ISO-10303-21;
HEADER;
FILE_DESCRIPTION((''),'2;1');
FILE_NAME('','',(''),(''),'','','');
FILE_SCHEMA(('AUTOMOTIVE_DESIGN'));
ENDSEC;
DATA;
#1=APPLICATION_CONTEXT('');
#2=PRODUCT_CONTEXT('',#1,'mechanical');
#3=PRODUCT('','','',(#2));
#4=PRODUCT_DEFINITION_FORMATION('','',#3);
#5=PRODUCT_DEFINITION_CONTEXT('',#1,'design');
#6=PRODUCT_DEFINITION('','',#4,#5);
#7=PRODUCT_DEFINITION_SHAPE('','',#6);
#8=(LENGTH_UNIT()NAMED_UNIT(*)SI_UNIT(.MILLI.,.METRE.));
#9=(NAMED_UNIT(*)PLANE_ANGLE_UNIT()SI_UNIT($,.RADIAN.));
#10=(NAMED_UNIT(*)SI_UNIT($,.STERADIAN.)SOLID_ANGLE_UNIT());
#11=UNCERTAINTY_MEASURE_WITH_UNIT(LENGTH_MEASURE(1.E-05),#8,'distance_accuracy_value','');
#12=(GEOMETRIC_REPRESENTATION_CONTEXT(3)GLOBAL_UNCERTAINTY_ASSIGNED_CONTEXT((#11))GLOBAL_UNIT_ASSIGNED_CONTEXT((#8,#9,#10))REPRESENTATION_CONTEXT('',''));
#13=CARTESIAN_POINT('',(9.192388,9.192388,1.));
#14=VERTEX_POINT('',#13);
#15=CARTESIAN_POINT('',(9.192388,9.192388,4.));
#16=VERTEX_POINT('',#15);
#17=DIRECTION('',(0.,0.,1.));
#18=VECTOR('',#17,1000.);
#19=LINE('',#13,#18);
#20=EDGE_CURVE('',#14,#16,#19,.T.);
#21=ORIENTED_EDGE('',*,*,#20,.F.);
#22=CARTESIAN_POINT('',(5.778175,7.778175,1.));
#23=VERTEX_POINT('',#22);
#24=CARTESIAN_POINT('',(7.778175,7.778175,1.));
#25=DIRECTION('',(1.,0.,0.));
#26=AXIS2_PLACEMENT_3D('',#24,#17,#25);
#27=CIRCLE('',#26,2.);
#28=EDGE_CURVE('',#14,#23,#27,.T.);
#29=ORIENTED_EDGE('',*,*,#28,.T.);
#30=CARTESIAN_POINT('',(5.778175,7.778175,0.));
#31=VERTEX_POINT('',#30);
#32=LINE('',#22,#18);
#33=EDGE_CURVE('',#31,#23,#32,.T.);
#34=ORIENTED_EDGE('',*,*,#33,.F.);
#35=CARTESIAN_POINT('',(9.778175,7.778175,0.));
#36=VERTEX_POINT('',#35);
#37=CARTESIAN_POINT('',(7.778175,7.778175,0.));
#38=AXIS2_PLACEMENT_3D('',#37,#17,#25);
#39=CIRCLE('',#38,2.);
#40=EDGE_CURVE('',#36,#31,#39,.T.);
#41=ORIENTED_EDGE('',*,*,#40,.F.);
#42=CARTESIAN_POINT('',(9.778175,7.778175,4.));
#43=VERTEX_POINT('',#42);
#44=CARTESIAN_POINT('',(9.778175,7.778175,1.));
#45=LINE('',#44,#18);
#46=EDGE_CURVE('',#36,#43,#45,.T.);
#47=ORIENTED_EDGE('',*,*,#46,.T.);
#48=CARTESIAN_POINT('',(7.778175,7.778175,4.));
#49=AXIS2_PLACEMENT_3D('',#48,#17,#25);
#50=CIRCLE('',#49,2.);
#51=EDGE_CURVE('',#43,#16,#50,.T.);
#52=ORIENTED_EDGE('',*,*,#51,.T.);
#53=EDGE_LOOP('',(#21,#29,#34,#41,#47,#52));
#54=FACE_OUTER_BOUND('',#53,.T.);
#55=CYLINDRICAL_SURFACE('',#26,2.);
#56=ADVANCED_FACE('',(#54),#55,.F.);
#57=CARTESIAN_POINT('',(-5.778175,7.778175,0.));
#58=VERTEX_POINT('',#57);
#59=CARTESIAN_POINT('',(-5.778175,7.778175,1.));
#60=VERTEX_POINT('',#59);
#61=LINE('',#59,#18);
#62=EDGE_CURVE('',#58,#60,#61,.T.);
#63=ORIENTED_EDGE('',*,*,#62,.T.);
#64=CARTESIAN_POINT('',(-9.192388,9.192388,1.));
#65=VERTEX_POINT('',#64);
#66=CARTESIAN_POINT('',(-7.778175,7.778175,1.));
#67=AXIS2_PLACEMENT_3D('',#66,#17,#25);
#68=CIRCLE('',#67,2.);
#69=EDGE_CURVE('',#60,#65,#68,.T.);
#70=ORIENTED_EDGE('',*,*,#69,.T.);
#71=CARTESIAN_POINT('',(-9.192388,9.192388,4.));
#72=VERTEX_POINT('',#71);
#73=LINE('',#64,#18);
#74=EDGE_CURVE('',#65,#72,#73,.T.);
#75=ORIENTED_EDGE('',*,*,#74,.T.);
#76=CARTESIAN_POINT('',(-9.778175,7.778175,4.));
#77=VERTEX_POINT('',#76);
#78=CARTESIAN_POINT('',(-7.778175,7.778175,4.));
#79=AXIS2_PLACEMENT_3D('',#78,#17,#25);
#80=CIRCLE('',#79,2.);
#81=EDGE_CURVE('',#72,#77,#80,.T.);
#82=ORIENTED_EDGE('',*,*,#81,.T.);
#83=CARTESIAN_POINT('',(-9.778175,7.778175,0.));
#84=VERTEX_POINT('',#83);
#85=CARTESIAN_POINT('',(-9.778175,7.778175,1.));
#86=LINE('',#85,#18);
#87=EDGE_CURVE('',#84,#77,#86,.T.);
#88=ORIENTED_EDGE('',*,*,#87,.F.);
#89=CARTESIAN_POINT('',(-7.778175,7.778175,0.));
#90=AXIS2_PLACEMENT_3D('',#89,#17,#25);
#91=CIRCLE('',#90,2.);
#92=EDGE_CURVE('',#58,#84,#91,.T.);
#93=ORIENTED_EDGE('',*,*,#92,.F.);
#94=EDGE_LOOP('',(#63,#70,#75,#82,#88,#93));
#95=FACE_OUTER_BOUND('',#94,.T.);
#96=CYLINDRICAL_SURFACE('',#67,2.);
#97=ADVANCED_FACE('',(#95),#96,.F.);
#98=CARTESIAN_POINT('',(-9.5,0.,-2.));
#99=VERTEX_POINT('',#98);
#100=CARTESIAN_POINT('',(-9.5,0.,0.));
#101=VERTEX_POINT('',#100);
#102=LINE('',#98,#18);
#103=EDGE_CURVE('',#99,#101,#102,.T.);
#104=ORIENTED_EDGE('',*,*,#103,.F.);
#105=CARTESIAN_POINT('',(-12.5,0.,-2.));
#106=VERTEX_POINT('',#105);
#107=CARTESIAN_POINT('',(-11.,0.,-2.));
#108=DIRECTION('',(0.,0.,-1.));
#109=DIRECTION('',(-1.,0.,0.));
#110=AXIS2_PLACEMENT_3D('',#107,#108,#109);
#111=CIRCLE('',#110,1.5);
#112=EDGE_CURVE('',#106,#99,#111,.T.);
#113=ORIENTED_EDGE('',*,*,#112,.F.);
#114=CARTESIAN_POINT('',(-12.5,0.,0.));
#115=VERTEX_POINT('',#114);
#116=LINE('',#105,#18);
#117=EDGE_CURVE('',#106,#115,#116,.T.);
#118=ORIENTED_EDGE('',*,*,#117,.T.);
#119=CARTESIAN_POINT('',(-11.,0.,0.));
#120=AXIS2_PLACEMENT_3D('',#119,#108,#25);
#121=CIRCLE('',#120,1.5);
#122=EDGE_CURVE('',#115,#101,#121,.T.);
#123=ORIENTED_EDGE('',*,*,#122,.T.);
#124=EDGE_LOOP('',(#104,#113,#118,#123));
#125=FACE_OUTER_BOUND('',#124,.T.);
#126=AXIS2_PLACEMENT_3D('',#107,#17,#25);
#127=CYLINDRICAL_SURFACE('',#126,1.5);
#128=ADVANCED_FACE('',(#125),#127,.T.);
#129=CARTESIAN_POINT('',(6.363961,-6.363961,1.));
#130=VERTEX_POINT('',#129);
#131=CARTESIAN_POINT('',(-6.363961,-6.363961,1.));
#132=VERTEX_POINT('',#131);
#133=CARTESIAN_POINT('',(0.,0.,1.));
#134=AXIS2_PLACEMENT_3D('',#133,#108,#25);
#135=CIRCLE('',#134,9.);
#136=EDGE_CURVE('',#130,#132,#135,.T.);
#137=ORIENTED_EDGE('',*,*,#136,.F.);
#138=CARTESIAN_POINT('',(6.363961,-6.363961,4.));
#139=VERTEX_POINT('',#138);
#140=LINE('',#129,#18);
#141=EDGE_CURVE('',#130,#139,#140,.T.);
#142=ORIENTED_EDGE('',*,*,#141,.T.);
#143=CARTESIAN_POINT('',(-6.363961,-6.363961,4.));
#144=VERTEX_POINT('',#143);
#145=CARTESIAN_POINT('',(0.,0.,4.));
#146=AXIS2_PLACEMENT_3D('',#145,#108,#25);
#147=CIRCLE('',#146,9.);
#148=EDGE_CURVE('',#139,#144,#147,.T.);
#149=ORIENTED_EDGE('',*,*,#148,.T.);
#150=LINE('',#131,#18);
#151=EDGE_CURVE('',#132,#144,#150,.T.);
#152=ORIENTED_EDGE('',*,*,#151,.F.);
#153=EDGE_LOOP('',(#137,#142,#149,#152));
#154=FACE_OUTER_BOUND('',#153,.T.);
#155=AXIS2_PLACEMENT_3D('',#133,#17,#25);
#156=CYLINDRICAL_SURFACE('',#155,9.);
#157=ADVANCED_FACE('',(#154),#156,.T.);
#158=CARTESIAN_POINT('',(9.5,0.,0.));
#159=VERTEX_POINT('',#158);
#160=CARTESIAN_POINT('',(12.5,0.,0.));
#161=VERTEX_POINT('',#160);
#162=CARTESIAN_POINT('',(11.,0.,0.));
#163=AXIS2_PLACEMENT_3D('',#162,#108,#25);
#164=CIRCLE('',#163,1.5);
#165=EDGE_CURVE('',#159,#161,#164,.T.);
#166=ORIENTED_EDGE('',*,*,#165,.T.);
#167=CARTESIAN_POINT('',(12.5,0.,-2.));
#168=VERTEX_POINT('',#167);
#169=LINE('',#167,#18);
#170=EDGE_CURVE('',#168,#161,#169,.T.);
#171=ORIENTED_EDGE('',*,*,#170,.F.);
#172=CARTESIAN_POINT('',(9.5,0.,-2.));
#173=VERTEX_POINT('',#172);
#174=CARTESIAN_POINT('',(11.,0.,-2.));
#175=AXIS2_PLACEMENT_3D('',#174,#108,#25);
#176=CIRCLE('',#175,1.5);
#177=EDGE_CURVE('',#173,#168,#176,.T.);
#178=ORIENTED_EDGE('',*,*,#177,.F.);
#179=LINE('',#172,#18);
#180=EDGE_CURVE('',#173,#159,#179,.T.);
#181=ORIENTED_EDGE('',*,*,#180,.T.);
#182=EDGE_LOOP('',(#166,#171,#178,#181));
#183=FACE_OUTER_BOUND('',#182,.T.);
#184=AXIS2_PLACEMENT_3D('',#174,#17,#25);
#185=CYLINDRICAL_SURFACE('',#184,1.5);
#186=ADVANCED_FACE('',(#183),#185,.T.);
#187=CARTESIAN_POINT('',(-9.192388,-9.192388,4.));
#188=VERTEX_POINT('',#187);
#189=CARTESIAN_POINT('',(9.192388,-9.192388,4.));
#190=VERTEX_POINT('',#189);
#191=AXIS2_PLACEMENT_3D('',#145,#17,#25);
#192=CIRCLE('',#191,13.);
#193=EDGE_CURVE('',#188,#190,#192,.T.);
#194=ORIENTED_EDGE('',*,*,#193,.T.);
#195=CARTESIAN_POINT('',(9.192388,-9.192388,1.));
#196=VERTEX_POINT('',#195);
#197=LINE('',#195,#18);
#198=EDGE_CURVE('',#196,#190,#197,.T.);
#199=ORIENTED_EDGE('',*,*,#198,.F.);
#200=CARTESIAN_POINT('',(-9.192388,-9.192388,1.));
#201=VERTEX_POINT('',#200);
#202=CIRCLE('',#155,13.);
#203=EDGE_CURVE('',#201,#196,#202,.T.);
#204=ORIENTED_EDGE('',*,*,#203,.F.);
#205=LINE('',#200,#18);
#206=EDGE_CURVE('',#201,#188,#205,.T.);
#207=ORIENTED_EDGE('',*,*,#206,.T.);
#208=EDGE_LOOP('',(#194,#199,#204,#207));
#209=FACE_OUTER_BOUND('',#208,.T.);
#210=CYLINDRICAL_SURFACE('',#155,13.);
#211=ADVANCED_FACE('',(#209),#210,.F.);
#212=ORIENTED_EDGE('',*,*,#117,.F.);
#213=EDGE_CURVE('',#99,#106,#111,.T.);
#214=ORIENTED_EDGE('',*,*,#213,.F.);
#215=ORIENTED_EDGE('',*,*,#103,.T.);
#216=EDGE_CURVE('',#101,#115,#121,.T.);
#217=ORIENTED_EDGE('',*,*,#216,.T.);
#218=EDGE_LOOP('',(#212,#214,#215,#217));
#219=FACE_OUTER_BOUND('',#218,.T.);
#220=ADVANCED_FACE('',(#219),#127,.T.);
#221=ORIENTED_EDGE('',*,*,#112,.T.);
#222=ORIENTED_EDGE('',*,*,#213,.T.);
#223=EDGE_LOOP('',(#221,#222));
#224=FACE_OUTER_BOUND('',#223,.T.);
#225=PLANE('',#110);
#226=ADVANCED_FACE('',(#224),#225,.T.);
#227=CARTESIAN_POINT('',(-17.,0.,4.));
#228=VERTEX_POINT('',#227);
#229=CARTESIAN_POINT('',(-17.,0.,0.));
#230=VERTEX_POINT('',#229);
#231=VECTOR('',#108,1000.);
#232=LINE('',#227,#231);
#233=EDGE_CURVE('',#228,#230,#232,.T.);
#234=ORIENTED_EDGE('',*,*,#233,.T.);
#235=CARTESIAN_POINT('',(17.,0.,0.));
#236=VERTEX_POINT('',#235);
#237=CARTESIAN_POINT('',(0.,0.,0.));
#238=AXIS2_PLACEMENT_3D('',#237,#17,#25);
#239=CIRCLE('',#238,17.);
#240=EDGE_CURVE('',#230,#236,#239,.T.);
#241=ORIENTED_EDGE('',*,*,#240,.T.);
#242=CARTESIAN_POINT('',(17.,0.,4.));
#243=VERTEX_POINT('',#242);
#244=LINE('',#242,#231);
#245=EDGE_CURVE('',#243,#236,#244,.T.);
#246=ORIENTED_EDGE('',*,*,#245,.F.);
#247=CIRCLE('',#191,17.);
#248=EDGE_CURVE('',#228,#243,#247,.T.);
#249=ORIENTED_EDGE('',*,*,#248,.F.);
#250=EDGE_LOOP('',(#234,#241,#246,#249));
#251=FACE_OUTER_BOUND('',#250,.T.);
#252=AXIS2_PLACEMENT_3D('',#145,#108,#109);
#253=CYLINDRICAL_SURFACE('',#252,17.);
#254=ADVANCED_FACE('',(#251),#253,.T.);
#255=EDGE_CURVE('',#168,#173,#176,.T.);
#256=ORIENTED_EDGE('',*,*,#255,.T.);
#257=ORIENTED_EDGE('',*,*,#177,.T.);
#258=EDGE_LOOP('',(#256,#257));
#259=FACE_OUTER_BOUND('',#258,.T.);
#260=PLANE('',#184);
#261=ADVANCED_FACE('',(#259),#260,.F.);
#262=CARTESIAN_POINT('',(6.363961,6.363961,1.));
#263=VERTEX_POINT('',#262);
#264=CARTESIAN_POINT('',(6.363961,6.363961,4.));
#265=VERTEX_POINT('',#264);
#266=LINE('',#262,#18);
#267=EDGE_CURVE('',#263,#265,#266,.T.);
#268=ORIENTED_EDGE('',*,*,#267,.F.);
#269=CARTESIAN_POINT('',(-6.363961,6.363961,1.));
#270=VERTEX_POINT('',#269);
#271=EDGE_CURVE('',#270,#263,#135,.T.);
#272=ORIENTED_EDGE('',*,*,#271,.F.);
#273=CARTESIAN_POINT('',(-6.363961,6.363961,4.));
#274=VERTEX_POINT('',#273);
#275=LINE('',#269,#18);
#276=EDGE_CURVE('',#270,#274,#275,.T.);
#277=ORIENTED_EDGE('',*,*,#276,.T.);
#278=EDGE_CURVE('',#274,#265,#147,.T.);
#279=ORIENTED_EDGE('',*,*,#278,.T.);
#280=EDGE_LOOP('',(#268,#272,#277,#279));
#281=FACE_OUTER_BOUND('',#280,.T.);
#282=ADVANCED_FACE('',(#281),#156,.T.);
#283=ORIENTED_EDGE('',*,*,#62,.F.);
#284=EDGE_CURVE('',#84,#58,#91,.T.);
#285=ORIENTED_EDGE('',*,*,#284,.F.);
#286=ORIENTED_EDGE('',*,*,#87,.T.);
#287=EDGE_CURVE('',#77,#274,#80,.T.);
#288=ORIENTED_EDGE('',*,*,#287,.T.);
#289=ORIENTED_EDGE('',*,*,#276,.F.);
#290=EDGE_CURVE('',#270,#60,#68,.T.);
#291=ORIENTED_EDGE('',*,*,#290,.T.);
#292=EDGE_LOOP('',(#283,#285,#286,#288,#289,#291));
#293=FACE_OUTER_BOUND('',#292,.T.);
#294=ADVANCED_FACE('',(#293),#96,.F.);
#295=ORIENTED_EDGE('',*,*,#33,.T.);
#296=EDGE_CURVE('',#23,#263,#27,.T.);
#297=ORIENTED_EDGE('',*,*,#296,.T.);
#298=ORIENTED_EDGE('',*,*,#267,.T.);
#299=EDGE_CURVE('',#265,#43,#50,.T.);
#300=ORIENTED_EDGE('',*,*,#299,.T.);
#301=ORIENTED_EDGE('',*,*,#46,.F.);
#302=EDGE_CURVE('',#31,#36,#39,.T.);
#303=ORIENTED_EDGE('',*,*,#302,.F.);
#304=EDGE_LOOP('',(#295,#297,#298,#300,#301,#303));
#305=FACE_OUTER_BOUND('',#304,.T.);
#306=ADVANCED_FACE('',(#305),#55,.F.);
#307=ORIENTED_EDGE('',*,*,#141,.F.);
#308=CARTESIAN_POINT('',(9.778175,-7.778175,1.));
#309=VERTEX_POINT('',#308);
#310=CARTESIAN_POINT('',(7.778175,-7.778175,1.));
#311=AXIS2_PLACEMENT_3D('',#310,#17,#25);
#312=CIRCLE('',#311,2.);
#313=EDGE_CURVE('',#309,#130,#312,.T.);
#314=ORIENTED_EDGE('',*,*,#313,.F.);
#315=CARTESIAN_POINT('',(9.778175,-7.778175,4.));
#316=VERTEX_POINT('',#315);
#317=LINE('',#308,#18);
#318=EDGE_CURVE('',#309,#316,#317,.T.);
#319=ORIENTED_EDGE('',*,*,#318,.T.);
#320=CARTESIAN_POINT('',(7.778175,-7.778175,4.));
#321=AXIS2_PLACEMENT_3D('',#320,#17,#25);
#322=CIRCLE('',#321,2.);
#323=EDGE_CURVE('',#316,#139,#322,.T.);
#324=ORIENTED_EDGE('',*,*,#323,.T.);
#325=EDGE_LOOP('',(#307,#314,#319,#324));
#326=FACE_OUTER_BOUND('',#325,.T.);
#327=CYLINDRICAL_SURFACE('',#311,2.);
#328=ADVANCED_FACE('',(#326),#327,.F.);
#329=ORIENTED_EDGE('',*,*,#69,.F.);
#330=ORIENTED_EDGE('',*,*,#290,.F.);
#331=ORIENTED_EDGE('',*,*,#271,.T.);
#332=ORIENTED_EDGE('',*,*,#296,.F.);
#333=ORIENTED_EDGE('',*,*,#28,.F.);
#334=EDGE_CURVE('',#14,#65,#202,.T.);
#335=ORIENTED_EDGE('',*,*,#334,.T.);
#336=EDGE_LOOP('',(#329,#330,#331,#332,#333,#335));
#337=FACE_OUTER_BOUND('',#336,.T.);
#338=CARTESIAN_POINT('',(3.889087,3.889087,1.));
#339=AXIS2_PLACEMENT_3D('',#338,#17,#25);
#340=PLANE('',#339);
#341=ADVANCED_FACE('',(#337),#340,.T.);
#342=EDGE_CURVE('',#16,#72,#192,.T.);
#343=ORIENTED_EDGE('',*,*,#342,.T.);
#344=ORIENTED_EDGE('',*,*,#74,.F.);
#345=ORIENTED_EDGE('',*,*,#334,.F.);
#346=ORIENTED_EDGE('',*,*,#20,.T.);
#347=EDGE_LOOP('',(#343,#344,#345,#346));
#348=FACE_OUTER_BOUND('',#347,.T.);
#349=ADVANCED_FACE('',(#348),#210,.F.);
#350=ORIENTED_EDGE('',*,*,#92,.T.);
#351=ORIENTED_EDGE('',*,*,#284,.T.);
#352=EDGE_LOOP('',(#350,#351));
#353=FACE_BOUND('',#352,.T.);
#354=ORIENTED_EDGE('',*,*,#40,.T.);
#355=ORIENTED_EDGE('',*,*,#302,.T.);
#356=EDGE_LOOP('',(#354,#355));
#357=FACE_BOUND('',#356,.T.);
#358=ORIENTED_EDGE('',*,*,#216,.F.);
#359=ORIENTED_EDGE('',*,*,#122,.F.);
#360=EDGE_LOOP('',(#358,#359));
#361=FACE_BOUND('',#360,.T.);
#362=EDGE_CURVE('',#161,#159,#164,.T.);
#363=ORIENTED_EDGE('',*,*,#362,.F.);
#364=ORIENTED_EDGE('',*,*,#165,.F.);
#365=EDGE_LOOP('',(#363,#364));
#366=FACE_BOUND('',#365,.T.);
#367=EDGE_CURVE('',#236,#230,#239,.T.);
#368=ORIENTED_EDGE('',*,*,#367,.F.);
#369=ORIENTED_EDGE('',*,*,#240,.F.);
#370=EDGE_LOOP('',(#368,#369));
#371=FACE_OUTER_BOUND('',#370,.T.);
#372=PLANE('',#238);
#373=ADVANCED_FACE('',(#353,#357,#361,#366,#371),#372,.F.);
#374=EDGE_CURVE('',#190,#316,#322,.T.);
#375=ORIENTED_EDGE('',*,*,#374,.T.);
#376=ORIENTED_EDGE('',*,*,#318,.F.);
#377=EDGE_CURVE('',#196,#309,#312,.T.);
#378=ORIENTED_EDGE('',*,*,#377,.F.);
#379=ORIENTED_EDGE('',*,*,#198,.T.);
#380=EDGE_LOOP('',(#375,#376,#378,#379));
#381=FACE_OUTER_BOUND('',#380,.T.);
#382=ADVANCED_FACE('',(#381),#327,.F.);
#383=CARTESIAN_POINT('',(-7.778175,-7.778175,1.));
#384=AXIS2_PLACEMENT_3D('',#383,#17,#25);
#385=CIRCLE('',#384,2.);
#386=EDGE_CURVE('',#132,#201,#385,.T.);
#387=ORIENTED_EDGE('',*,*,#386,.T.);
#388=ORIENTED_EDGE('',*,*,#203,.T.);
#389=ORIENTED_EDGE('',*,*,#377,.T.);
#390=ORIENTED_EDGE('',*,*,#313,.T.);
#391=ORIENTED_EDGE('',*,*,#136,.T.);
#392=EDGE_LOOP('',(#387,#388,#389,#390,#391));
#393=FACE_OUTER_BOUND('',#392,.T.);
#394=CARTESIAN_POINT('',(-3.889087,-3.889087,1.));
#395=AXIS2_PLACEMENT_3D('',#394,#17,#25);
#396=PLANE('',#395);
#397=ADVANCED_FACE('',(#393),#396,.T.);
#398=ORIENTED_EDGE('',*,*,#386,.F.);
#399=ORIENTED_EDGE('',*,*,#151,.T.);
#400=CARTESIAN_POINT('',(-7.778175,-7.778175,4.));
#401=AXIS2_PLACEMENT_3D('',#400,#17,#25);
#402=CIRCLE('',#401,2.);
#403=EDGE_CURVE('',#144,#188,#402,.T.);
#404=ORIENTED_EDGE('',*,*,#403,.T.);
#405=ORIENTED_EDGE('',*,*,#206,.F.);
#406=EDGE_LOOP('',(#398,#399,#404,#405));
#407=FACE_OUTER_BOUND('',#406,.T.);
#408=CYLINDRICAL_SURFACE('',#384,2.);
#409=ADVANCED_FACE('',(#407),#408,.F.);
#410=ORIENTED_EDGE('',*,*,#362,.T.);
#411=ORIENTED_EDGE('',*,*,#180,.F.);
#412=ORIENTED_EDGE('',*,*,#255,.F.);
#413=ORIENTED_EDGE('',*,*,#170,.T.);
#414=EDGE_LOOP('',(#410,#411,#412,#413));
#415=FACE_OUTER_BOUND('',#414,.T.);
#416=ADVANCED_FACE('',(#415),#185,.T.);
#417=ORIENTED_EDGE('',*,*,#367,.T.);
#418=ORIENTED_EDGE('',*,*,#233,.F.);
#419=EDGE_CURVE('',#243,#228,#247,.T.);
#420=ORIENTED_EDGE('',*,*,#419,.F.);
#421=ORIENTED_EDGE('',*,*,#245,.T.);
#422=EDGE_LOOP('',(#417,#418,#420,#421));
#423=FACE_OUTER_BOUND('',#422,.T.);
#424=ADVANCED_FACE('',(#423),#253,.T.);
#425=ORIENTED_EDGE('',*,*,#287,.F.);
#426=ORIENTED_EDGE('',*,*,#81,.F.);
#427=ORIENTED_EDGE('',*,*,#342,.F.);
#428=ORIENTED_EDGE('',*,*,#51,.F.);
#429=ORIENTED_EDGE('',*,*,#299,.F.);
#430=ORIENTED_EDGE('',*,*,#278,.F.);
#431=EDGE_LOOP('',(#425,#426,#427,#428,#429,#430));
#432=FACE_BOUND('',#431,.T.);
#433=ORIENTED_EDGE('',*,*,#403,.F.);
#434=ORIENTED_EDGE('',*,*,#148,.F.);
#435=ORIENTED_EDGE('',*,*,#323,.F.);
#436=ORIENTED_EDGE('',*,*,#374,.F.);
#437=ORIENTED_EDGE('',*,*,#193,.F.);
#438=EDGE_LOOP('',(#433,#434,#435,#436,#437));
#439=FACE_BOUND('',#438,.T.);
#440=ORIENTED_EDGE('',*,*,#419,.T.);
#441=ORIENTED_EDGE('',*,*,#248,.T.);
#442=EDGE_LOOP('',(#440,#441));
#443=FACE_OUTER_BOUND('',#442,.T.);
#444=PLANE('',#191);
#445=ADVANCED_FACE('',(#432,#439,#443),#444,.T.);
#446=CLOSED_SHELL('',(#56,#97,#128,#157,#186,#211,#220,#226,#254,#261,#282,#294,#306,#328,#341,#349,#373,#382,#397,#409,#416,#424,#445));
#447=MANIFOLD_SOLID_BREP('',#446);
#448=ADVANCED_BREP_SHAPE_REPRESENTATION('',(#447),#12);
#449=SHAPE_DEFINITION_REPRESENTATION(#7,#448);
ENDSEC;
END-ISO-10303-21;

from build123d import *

# Parameters (mm, degrees)
SKETCH1_R           = 17
BOSS_EXTRUDE1_DEPTH = 4
CUT_EXTRUDE1_DEPTH  = 3
SKETCH3_R           = 2
CUT_EXTRUDE2_DEPTH  = 4
CUT_EXTRUDE3_DEPTH  = 3
SKETCH7_R           = 1.5
BOSS_EXTRUDE3_DEPTH = 2


with BuildPart() as part:
    # Sketch1 → Boss-Extrude1 (new body)
    with BuildSketch(Plane.XY):
        Circle(SKETCH1_R)
    extrude(amount=BOSS_EXTRUDE1_DEPTH)

    # Sketch2 → Cut-Extrude1 (cut)
    with BuildSketch(Plane.XY.offset(4)):
        with BuildLine():
            ThreePointArc((9.192388155, 9.192388155), (0, 13), (-9.192388155, 9.192388155))
            ThreePointArc((-9.192388155, 9.192388155), (-9.192388155, 6.363961031), (-6.363961031, 6.363961031))
            ThreePointArc((-6.363961031, 6.363961031), (0, 9), (6.363961031, 6.363961031))
            ThreePointArc((6.363961031, 6.363961031), (9.192388155, 6.363961031), (9.192388155, 9.192388155))
        make_face()
    extrude(amount=-CUT_EXTRUDE1_DEPTH, mode=Mode.SUBTRACT)

    # Sketch3 → Cut-Extrude2 (cut)
    with BuildSketch(Plane.XY.offset(4)):
        with Locations((7.778174593, 7.778174593)):
            Circle(SKETCH3_R)
        with Locations((-7.778174593, 7.778174593)):
            Circle(SKETCH3_R)
    extrude(amount=-CUT_EXTRUDE2_DEPTH, mode=Mode.SUBTRACT)

    # Sketch4 → Cut-Extrude3 (cut)
    with BuildSketch(Plane.XY.offset(4)):
        with BuildLine():
            ThreePointArc((-9.192388155, -9.192388155), (0, -13), (9.192388155, -9.192388155))
            ThreePointArc((9.192388155, -9.192388155), (9.192388155, -6.363961031), (6.363961031, -6.363961031))
            ThreePointArc((6.363961031, -6.363961031), (0, -9), (-6.363961031, -6.363961031))
            ThreePointArc((-6.363961031, -6.363961031), (-9.192388155, -6.363961031), (-9.192388155, -9.192388155))
        make_face()
    extrude(amount=-CUT_EXTRUDE3_DEPTH, mode=Mode.SUBTRACT)

    # Sketch7 → Boss-Extrude3 (add)
    with BuildSketch(Plane(origin=(0, 0, 0), x_dir=(-1, 0, 0), z_dir=(0, 0, -1))):
        with Locations(Location((11, 0, 0), (0, 0, 180))):
            Circle(SKETCH7_R)
        with Locations(Location((-11, 0, 0), (0, 0, 180))):
            Circle(SKETCH7_R)
    extrude(amount=BOSS_EXTRUDE3_DEPTH)


solid = part.part
